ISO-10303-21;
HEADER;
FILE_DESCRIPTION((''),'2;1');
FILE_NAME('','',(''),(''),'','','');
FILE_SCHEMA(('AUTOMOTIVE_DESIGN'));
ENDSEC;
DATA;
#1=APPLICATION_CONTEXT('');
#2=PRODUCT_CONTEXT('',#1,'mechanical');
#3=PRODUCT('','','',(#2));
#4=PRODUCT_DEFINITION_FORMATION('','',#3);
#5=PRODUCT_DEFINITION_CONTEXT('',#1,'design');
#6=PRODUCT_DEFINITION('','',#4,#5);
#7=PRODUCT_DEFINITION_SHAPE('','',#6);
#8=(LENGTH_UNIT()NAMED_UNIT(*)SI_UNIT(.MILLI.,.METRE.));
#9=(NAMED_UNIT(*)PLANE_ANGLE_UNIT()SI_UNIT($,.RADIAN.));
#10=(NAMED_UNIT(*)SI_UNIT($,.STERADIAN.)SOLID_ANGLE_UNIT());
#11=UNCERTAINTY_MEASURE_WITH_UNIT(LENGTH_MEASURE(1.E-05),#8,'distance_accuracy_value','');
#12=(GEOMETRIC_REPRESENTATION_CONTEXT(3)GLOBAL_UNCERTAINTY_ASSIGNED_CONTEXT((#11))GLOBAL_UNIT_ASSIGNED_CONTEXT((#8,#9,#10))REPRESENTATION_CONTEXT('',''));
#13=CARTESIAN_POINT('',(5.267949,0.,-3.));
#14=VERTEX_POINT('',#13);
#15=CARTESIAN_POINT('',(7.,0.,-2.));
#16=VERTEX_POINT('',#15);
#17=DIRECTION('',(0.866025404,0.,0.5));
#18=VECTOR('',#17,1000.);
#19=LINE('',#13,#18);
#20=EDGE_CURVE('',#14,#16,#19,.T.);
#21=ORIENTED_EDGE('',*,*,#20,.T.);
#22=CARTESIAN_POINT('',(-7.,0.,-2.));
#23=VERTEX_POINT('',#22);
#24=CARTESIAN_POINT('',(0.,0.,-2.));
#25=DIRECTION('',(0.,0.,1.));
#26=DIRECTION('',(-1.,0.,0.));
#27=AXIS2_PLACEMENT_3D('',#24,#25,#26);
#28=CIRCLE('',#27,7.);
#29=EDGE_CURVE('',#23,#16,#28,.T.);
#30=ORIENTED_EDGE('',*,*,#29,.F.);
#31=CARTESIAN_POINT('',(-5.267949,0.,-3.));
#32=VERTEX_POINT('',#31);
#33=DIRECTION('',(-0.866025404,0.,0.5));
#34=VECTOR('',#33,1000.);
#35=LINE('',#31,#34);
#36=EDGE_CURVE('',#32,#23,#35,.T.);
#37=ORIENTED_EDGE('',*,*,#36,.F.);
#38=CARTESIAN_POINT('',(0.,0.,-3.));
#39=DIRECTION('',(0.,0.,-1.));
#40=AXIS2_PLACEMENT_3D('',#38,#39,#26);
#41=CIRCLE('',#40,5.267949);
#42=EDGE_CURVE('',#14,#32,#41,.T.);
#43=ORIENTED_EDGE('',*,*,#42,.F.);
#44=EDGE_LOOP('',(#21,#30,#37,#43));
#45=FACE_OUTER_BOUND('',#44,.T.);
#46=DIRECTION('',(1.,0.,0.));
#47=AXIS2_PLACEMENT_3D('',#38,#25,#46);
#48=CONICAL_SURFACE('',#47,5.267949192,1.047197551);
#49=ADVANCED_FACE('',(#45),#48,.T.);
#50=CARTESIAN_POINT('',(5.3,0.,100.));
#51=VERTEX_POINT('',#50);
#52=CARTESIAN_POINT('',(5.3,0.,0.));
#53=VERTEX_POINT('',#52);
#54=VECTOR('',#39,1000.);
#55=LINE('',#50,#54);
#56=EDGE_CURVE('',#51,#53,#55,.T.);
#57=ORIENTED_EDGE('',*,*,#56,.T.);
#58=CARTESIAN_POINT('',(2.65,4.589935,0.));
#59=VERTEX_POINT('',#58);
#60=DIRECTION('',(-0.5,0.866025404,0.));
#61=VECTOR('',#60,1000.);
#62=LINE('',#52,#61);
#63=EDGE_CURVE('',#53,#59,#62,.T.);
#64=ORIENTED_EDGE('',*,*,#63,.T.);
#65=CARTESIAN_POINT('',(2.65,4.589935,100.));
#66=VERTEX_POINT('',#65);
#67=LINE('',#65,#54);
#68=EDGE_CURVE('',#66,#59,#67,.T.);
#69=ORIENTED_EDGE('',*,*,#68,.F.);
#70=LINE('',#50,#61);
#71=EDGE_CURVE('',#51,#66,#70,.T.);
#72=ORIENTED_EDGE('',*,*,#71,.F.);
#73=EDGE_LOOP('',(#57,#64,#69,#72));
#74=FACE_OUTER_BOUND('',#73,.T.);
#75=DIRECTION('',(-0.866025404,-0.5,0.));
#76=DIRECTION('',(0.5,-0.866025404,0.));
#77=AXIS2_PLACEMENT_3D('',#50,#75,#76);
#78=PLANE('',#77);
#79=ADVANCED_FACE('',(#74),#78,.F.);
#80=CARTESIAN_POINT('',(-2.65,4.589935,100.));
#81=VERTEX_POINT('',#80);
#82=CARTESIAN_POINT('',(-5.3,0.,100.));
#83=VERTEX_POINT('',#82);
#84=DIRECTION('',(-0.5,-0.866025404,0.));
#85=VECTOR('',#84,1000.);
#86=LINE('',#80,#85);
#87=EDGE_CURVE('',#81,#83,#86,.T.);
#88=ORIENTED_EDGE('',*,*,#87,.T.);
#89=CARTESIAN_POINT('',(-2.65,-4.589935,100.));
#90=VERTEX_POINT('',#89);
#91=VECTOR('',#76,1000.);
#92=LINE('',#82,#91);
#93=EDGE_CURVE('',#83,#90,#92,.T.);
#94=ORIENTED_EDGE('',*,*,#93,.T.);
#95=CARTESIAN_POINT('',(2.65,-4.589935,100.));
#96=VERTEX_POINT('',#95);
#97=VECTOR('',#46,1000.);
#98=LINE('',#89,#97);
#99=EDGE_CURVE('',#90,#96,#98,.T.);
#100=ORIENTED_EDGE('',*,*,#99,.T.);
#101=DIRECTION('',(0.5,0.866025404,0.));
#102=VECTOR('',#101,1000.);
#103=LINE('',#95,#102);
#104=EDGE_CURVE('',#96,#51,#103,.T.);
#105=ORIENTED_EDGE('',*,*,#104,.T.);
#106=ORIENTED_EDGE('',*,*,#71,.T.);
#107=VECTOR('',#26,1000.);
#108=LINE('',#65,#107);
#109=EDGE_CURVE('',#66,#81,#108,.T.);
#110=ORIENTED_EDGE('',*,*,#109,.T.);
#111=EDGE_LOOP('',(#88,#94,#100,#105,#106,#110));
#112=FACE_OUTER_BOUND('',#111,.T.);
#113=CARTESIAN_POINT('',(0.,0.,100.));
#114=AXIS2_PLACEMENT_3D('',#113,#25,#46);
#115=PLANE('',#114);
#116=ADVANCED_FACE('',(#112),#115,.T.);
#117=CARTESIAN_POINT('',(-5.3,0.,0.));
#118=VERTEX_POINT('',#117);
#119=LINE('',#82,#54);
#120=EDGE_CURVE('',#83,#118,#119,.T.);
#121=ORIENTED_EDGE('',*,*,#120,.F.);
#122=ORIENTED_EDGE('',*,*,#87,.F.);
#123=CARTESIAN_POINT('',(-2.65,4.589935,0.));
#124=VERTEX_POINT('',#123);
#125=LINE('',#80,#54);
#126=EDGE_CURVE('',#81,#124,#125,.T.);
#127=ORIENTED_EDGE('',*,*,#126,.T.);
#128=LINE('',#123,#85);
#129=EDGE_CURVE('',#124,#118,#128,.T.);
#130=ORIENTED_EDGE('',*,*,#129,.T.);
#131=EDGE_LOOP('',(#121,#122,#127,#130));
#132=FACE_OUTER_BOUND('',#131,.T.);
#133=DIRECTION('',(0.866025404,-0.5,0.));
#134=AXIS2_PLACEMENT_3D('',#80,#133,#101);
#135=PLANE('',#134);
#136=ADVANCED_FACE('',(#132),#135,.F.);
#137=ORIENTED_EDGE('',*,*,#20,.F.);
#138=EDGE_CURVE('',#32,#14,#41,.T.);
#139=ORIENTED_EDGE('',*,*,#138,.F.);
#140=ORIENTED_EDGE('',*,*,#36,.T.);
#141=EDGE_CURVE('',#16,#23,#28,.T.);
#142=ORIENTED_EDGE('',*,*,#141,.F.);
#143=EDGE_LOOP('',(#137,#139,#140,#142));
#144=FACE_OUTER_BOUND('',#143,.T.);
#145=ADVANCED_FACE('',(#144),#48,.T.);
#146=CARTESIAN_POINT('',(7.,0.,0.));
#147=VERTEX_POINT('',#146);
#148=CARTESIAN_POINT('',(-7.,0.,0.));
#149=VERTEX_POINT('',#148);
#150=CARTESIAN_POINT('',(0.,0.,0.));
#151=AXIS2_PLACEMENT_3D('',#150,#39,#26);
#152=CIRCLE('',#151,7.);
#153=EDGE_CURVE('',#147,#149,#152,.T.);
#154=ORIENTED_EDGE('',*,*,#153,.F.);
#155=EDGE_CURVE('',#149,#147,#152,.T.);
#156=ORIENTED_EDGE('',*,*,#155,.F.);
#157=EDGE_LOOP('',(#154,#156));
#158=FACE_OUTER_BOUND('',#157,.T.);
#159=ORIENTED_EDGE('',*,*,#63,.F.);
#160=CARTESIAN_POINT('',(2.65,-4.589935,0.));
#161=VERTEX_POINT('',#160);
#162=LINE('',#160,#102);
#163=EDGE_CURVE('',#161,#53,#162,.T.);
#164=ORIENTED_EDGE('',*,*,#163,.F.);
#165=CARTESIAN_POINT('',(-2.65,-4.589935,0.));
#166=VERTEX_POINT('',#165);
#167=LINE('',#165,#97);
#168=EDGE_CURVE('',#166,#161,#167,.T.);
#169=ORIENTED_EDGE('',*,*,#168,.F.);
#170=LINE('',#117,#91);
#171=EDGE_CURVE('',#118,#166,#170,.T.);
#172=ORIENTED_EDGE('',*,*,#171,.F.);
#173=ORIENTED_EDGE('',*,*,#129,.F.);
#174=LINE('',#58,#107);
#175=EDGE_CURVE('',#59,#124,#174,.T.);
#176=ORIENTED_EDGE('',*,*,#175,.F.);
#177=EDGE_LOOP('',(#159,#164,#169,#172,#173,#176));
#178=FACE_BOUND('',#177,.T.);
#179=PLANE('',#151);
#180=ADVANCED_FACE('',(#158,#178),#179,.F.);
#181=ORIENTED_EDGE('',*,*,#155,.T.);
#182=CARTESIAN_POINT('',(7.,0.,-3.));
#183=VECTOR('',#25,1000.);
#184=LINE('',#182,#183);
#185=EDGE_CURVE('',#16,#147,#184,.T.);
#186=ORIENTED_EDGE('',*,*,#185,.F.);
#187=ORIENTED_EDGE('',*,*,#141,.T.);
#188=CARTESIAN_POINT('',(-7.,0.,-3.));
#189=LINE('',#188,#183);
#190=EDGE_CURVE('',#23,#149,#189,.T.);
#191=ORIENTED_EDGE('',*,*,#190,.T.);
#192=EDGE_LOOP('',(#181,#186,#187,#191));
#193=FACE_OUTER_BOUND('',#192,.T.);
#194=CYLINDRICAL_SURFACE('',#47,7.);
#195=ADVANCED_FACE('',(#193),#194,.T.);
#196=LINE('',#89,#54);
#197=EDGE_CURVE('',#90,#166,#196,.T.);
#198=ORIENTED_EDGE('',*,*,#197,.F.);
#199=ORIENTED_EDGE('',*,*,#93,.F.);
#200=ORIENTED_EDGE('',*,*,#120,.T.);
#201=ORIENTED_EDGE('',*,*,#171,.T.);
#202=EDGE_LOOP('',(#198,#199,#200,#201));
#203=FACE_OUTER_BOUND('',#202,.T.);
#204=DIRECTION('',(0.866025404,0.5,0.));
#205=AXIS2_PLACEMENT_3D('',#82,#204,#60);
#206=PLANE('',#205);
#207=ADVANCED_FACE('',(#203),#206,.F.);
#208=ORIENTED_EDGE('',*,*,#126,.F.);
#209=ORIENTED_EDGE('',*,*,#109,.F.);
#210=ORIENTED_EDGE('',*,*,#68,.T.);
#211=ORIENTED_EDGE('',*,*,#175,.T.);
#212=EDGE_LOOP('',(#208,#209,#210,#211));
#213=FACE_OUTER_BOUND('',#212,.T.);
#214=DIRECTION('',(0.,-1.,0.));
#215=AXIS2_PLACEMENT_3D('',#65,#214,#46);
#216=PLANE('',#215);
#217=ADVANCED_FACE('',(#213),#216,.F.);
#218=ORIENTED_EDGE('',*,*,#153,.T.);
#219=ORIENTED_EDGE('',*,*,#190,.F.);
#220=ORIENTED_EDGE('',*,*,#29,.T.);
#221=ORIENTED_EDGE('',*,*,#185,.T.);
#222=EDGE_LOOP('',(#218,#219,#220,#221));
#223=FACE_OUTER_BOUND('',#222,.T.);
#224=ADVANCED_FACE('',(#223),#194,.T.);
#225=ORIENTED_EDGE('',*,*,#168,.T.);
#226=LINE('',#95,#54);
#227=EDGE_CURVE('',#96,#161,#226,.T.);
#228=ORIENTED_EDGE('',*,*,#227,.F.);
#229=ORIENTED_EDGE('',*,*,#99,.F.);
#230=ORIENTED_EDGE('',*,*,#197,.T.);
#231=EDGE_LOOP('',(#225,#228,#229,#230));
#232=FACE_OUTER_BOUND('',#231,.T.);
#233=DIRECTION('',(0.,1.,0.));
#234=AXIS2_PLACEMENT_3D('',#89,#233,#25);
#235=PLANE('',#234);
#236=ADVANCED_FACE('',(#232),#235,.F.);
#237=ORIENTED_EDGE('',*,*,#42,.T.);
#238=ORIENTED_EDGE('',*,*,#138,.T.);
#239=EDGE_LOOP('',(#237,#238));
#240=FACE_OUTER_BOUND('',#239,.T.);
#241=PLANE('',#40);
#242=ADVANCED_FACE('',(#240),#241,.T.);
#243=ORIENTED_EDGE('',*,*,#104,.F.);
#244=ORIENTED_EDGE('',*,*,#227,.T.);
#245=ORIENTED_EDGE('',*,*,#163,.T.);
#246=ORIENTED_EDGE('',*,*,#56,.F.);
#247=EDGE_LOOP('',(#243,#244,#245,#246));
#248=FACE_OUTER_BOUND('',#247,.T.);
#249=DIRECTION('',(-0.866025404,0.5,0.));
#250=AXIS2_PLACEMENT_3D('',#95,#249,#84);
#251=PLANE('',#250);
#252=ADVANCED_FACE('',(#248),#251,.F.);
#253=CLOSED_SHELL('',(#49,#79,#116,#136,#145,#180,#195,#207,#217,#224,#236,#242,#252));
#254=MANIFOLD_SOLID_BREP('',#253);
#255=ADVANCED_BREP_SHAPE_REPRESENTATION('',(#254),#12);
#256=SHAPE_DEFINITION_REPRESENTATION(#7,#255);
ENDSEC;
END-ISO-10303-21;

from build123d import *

# Parameters (mm, degrees)
BOSS_EXTRUDE1_DEPTH = 100
SKETCH2_R           = 7
BOSS_EXTRUDE2_DEPTH = 3
CHAMFER1_SIZE       = 1
CHAMFER1_SIZE2      = 1.732050808


with BuildPart() as part:
    # Sketch1 → Boss-Extrude1 (new body)
    with BuildSketch(Plane.XY):
        Polygon((2.65, -4.58993464), (5.3, 0), (2.65, 4.58993464), (-2.65, 4.58993464), (-5.3, 0), (-2.65, -4.58993464), align=None)
    extrude(amount=BOSS_EXTRUDE1_DEPTH)

    # Sketch2 → Boss-Extrude2 (add)
    with BuildSketch(Plane(origin=(0, 0, 0), x_dir=(-1, 0, 0), z_dir=(0, 0, -1))):
        Circle(SKETCH2_R)
    extrude(amount=BOSS_EXTRUDE2_DEPTH)

    # Chamfer1
    chamfer1_edges = [part.edges().sort_by_distance(p)[0] for p in [
        (7, 0, -3),
    ]]
    chamfer1_side = [part.faces().sort_by_distance(p)[0] for p in [
        (7, 0, -1.5),
    ]]
    chamfer(chamfer1_edges, length=CHAMFER1_SIZE, length2=CHAMFER1_SIZE2, reference=chamfer1_side[0])


solid = part.part
